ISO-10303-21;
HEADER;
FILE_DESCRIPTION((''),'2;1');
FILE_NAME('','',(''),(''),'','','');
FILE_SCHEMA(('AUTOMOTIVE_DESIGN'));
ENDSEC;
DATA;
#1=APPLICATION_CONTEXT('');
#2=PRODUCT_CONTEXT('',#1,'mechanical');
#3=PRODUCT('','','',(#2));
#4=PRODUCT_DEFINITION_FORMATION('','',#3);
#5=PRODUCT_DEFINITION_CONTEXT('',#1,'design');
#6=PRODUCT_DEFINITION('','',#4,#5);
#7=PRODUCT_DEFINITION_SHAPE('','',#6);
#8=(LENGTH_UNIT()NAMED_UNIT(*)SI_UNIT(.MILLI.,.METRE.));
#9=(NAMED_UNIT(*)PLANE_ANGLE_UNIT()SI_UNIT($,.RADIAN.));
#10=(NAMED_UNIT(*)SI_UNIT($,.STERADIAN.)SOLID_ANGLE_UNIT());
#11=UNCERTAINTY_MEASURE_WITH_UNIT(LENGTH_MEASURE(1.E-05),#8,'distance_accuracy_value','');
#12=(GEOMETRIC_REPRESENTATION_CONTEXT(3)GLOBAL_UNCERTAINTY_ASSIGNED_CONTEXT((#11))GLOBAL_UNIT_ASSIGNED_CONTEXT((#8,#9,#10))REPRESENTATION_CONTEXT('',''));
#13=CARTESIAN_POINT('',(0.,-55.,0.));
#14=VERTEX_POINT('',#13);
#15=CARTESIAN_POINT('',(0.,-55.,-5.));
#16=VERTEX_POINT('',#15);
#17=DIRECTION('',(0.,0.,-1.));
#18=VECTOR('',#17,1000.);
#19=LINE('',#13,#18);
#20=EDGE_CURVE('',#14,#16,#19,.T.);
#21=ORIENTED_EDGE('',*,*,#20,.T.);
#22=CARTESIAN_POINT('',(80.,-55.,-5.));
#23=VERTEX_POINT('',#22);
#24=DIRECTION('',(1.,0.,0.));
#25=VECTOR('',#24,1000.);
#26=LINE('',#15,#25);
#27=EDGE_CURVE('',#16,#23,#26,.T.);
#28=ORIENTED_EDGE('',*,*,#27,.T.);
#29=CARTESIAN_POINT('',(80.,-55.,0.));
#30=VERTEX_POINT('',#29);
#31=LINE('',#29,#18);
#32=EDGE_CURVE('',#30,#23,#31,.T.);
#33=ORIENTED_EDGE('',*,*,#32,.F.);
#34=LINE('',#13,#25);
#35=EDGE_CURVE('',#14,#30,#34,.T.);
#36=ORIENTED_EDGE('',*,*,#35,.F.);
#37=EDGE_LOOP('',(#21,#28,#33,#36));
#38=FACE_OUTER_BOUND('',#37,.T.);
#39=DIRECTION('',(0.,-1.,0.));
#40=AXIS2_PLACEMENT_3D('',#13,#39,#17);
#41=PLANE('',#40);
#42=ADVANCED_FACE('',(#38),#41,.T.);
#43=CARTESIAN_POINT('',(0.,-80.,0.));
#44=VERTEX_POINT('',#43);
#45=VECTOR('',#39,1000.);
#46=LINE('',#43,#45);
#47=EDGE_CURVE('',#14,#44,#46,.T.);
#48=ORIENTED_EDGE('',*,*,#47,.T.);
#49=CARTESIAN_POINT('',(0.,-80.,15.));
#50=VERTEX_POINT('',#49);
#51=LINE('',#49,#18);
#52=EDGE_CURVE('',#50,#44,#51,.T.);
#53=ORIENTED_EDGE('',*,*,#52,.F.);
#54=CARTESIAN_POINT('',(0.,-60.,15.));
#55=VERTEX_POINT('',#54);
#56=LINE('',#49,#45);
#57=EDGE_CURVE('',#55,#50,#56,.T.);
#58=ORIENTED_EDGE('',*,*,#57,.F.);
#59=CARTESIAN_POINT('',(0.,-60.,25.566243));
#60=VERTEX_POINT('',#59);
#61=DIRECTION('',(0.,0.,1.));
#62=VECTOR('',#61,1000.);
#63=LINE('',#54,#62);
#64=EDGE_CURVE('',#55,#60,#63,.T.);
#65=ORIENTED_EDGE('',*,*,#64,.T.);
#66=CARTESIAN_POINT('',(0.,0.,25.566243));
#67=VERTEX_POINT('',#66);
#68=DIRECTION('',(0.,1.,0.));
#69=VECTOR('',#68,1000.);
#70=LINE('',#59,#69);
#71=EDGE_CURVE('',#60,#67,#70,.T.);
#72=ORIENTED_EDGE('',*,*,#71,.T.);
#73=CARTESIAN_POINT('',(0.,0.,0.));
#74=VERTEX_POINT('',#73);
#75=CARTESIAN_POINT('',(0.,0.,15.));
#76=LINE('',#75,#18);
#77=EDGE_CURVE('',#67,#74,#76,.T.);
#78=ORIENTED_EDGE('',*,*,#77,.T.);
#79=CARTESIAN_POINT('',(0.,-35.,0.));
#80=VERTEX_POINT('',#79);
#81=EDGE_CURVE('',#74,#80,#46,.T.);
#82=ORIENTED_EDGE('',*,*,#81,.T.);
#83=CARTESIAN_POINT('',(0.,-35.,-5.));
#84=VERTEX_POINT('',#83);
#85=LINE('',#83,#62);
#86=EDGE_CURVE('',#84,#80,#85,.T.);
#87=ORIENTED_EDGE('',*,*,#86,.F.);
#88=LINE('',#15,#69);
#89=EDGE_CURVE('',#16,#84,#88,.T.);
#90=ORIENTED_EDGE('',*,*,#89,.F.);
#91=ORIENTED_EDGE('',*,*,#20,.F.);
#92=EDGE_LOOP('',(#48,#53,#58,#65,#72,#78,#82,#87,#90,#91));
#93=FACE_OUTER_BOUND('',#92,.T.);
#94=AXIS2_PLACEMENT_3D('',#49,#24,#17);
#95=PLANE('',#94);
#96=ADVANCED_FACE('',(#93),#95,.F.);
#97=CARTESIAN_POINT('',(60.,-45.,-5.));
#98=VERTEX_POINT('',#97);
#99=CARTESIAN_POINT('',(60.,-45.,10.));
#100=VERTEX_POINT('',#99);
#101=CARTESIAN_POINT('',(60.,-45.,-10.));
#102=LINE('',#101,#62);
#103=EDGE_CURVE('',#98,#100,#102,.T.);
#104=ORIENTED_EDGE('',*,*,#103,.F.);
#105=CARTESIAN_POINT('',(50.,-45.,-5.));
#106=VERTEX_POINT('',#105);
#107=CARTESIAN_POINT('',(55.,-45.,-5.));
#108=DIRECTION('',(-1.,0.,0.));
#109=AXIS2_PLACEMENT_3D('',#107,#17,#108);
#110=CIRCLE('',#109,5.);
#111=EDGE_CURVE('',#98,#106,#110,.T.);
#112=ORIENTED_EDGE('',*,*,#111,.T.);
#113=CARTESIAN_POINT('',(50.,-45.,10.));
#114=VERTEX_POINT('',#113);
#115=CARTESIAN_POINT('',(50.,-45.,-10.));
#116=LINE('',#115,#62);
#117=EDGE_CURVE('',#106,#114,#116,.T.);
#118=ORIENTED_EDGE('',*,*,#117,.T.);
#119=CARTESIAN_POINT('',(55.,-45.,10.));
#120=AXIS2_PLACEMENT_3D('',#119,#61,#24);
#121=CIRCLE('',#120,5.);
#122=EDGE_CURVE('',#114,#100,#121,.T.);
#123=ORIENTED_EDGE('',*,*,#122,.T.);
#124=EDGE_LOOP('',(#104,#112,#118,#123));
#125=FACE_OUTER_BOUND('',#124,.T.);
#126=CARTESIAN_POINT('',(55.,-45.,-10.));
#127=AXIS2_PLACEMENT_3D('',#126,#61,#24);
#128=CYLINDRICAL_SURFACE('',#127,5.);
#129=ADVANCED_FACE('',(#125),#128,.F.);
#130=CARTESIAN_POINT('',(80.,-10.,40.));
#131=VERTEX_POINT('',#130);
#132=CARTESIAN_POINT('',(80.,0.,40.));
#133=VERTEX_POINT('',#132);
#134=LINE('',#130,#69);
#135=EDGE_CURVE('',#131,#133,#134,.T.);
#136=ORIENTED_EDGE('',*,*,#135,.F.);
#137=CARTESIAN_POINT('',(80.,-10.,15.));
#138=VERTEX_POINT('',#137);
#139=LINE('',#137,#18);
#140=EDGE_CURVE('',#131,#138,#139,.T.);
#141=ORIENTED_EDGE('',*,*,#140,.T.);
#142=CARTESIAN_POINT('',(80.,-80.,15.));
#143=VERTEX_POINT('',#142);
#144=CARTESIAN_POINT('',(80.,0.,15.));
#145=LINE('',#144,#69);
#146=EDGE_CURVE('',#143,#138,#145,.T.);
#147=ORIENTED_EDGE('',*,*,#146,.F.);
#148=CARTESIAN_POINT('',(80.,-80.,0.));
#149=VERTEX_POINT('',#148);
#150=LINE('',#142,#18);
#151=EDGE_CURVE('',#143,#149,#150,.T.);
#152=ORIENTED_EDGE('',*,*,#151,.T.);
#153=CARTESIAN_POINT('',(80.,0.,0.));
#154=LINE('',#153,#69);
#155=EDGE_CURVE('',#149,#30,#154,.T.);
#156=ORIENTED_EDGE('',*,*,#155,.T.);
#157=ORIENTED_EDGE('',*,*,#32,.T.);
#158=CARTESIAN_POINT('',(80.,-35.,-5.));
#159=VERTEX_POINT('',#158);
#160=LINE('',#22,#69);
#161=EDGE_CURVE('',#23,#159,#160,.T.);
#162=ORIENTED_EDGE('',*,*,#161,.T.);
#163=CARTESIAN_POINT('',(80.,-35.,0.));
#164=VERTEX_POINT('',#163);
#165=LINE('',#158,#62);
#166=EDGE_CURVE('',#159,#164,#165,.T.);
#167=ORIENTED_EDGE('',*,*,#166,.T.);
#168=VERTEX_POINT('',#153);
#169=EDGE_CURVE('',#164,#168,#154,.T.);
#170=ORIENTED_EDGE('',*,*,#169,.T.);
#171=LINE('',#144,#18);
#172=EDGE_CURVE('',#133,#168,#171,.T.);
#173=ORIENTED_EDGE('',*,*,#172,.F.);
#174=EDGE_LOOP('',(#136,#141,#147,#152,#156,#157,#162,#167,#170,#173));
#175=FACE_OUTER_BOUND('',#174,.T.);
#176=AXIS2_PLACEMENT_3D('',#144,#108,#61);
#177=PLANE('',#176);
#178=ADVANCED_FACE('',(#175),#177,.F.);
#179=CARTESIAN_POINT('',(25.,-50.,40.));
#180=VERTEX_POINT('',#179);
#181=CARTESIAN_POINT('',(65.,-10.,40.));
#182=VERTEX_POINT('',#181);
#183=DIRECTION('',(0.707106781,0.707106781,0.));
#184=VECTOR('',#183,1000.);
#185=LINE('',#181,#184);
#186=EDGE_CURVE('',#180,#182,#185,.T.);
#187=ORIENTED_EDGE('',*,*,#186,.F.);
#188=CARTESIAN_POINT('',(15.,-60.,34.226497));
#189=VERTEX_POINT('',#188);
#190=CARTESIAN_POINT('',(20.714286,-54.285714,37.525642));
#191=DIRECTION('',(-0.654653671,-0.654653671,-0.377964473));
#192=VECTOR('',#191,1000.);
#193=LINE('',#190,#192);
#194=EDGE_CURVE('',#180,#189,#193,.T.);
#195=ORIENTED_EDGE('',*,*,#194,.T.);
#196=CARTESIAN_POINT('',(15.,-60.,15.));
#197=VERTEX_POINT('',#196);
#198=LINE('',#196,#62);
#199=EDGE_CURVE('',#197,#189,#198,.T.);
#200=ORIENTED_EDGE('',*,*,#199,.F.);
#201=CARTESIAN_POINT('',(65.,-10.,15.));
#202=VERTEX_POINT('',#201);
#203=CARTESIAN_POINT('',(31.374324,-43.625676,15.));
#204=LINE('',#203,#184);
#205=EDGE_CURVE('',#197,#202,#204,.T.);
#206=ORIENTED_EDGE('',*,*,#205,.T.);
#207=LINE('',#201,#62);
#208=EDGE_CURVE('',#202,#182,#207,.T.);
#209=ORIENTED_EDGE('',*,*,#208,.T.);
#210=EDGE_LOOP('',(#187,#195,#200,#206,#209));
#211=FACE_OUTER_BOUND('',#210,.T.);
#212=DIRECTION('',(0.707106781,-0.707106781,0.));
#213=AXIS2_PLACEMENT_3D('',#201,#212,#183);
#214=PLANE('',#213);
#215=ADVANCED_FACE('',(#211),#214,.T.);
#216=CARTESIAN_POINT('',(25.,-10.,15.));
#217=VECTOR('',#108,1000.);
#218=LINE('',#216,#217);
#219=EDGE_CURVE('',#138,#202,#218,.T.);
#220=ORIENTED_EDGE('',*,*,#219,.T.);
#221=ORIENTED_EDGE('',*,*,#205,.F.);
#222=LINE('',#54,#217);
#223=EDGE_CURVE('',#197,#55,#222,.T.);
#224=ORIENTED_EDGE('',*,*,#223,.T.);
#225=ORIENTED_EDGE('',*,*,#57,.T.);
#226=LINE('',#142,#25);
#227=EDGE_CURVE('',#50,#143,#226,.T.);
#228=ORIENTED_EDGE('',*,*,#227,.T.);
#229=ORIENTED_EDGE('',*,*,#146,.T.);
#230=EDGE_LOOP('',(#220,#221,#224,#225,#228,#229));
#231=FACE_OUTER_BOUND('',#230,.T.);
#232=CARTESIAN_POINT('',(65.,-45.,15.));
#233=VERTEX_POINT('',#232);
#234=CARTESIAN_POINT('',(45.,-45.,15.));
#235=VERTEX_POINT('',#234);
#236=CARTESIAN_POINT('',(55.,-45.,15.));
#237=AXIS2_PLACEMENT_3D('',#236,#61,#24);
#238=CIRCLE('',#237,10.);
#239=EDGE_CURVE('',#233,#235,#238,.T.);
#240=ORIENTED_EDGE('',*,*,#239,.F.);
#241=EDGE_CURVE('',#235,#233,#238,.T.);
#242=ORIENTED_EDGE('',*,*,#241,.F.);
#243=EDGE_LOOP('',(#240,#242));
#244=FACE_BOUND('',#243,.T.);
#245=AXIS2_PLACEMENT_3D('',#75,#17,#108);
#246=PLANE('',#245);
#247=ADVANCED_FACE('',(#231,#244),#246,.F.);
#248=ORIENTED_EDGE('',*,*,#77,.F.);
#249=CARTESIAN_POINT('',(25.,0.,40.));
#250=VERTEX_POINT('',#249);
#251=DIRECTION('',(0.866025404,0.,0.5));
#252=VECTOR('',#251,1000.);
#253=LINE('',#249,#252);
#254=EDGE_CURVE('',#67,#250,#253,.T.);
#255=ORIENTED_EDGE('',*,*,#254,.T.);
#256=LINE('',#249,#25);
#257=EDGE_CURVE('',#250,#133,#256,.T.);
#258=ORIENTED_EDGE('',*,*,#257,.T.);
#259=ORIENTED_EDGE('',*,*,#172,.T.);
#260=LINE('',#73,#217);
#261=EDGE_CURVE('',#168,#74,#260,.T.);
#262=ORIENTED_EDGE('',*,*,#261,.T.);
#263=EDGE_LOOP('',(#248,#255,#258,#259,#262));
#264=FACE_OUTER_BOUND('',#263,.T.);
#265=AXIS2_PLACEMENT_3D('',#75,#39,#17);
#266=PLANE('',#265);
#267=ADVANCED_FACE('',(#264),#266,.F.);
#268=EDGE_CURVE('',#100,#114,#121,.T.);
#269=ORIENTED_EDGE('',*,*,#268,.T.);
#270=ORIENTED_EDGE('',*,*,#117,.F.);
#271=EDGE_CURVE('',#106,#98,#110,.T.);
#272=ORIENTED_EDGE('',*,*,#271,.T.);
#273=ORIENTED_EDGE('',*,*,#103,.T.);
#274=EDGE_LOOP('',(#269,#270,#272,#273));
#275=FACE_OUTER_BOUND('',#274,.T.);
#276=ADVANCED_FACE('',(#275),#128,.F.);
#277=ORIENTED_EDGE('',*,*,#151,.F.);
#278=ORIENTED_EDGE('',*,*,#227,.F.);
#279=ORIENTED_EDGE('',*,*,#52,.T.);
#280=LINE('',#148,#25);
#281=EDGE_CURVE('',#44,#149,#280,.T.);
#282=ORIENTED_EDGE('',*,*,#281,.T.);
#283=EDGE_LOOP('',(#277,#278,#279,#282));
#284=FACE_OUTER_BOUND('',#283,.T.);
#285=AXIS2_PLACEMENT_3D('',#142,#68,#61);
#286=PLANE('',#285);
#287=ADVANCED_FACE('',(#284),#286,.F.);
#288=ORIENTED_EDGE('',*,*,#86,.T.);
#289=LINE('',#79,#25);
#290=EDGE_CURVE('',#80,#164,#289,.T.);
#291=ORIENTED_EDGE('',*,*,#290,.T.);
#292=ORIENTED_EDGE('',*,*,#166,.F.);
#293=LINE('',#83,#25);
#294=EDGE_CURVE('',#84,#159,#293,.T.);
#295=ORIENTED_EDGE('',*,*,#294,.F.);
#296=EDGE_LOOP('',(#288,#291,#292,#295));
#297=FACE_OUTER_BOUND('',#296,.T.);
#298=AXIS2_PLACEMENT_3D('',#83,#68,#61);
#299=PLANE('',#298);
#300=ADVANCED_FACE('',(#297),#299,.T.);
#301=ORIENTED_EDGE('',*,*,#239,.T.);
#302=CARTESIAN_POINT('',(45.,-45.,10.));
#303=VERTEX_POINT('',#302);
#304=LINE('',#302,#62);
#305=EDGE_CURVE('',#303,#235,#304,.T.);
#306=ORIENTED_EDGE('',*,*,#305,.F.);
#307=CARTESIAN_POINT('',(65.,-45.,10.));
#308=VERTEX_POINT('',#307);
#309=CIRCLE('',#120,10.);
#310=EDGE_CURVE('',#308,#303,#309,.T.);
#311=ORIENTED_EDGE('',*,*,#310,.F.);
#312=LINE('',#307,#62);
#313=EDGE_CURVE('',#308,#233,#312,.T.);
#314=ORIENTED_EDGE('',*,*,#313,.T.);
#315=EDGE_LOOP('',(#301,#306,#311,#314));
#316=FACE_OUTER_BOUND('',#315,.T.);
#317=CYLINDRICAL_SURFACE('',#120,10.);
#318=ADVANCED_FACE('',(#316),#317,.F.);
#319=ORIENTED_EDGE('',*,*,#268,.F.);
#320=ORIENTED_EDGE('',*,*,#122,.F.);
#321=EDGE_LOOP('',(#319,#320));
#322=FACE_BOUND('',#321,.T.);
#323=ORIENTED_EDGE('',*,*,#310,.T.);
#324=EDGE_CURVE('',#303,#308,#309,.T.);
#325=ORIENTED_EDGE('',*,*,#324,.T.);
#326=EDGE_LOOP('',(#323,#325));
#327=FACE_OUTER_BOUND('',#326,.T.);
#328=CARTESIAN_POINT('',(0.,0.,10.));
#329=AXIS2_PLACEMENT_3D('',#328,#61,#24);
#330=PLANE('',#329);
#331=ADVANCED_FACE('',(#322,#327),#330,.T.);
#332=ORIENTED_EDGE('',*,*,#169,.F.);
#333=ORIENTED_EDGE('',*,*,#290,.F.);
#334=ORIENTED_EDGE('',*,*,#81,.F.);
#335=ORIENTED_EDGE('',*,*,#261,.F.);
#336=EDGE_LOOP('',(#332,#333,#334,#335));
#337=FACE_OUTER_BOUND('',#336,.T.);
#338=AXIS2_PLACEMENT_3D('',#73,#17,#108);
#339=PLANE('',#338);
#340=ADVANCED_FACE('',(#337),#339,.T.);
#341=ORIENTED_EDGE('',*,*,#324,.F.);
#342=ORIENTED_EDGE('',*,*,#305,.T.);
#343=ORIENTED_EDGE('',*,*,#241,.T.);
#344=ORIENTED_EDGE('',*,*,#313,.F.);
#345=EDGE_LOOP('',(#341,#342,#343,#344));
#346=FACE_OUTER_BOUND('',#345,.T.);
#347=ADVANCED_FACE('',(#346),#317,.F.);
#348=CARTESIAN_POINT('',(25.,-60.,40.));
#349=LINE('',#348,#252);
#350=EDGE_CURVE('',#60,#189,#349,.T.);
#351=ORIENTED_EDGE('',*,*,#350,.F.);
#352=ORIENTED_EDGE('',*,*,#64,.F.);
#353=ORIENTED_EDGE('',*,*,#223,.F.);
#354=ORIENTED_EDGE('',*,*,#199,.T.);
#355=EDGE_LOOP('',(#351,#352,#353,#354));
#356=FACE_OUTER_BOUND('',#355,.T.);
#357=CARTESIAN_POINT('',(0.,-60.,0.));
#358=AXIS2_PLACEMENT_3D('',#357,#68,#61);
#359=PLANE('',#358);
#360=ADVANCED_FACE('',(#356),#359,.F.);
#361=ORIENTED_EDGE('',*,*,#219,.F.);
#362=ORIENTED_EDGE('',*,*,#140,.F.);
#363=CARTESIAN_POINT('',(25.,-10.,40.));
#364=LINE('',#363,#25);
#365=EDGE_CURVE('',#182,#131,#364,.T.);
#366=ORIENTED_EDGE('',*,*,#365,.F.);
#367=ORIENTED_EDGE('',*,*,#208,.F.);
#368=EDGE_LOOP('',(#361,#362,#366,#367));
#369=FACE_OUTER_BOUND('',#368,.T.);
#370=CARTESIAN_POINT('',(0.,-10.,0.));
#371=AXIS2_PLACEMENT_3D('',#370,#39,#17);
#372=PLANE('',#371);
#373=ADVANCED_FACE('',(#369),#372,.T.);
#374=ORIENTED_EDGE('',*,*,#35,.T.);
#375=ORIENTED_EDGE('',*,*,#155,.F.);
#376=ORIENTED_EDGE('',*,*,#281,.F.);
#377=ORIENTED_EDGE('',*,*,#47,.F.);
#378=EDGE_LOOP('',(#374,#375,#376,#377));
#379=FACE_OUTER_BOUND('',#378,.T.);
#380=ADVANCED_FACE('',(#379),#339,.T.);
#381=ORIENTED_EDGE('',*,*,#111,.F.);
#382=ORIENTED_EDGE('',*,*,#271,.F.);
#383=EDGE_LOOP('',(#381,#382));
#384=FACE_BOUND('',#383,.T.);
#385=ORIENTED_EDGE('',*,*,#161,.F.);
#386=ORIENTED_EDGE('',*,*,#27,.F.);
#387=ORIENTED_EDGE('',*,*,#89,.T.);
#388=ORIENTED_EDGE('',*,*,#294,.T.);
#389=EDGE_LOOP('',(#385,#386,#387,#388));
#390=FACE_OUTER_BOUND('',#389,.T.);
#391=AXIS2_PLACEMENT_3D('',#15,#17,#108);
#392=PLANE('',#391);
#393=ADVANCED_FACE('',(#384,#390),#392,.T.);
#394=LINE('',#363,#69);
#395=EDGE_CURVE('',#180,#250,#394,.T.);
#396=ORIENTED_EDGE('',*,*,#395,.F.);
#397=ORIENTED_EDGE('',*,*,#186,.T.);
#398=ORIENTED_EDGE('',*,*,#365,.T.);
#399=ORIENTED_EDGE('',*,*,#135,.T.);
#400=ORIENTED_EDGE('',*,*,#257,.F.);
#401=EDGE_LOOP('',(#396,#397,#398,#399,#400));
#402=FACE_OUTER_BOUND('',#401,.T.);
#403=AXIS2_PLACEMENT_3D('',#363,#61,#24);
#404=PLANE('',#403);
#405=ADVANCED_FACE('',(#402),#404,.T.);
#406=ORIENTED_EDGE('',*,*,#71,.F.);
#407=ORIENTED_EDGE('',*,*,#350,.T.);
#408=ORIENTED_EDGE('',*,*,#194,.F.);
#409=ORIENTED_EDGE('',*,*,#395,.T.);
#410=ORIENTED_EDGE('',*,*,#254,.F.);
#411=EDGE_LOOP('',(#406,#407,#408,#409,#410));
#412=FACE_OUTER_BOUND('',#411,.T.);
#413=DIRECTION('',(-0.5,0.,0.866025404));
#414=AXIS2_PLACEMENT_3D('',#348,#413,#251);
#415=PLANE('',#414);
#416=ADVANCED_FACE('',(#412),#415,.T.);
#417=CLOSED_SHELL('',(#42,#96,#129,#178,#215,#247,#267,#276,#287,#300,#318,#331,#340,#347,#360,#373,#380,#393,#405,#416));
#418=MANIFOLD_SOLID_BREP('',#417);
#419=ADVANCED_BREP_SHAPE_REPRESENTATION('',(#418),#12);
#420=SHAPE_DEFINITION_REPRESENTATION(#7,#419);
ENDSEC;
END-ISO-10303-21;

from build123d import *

# Parameters (mm, degrees)
BASE_PLATE_SKETCH_W       = 80
BASE_PLATE_SKETCH_H       = 80
BASE_PLATE_80X80X15_DEPTH = 15
VERTICAL_WALL_SKETCH_W    = 5
VERTICAL_WALL_SKETCH_H    = 20
VERTICAL_WALL_DEPTH       = 80
STEP_BOSS_SKETCH_W        = 55
STEP_BOSS_SKETCH_H        = 25
STEP_BOSS_DEPTH           = 10
V_BLOCK_BODY_DEPTH        = 60
ANGLED_BOSS_45DEG_DEPTH   = 25
V_GROOVE_CUT_DEPTH        = 25
COUNTERBORE_SKETCH_R      = 10
COUNTERBORE_20X5_DEPTH    = 5
HOLE_SKETCH_R             = 5
HOLE_10_DEPTH             = 20


with BuildPart() as part:
    # Base Plate Sketch → Base Plate 80x80x15 (new body)
    with BuildSketch(Plane.XY):
        with Locations((40, -40)):
            Rectangle(BASE_PLATE_SKETCH_W, BASE_PLATE_SKETCH_H)
    extrude(amount=BASE_PLATE_80X80X15_DEPTH)

    # Vertical Wall Sketch → Vertical Wall (add)
    with BuildSketch(Plane(origin=(80, 0, 0), x_dir=(0, 0, -1), z_dir=(1, 0, 0))):
        with Locations((2.5, -45)):
            Rectangle(VERTICAL_WALL_SKETCH_W, VERTICAL_WALL_SKETCH_H)
    extrude(amount=-VERTICAL_WALL_DEPTH)

    # Step Boss Sketch → Step Boss (add)
    with BuildSketch(Plane(origin=(0, 0, 0), x_dir=(1, 0, 0), z_dir=(0, 1, 0))):
        with Locations((52.5, -27.5)):
            Rectangle(STEP_BOSS_SKETCH_W, STEP_BOSS_SKETCH_H)
    extrude(amount=-STEP_BOSS_DEPTH)

    # V Block Body Sketch → V Block Body (add)
    with BuildSketch(Plane(origin=(0, 0, 0), x_dir=(1, 0, 0), z_dir=(0, 1, 0))):
        Polygon((25, -40), (0, -25.56624327), (0, -15), (25, -15), align=None)
    extrude(amount=-V_BLOCK_BODY_DEPTH)

    # Angled Boss 45deg Sketch → Angled Boss 45deg (add)
    with BuildSketch(Plane.XY.offset(40)):
        Polygon((65, -10), (31.374324096, -43.625675904), (25, -50), (25, -10), align=None)
    extrude(amount=-ANGLED_BOSS_45DEG_DEPTH)

    # V Groove Sketch → V Groove Cut (cut)
    with BuildSketch(Plane.XY.offset(40)):
        Polygon((25, -50), (15, -60), (25, -60), align=None)
    extrude(amount=-V_GROOVE_CUT_DEPTH, mode=Mode.SUBTRACT)

    # Counterbore Sketch → Counterbore Ø20x5 (cut)
    with BuildSketch(Plane.XY.offset(15)):
        with Locations((55, -45)):
            Circle(COUNTERBORE_SKETCH_R)
    extrude(amount=-COUNTERBORE_20X5_DEPTH, mode=Mode.SUBTRACT)

    # Hole Sketch → Hole Ø10 (cut)
    with BuildSketch(Plane.XY.offset(10)):
        with Locations((55, -45)):
            Circle(HOLE_SKETCH_R)
    extrude(amount=-HOLE_10_DEPTH, mode=Mode.SUBTRACT)


solid = part.part
